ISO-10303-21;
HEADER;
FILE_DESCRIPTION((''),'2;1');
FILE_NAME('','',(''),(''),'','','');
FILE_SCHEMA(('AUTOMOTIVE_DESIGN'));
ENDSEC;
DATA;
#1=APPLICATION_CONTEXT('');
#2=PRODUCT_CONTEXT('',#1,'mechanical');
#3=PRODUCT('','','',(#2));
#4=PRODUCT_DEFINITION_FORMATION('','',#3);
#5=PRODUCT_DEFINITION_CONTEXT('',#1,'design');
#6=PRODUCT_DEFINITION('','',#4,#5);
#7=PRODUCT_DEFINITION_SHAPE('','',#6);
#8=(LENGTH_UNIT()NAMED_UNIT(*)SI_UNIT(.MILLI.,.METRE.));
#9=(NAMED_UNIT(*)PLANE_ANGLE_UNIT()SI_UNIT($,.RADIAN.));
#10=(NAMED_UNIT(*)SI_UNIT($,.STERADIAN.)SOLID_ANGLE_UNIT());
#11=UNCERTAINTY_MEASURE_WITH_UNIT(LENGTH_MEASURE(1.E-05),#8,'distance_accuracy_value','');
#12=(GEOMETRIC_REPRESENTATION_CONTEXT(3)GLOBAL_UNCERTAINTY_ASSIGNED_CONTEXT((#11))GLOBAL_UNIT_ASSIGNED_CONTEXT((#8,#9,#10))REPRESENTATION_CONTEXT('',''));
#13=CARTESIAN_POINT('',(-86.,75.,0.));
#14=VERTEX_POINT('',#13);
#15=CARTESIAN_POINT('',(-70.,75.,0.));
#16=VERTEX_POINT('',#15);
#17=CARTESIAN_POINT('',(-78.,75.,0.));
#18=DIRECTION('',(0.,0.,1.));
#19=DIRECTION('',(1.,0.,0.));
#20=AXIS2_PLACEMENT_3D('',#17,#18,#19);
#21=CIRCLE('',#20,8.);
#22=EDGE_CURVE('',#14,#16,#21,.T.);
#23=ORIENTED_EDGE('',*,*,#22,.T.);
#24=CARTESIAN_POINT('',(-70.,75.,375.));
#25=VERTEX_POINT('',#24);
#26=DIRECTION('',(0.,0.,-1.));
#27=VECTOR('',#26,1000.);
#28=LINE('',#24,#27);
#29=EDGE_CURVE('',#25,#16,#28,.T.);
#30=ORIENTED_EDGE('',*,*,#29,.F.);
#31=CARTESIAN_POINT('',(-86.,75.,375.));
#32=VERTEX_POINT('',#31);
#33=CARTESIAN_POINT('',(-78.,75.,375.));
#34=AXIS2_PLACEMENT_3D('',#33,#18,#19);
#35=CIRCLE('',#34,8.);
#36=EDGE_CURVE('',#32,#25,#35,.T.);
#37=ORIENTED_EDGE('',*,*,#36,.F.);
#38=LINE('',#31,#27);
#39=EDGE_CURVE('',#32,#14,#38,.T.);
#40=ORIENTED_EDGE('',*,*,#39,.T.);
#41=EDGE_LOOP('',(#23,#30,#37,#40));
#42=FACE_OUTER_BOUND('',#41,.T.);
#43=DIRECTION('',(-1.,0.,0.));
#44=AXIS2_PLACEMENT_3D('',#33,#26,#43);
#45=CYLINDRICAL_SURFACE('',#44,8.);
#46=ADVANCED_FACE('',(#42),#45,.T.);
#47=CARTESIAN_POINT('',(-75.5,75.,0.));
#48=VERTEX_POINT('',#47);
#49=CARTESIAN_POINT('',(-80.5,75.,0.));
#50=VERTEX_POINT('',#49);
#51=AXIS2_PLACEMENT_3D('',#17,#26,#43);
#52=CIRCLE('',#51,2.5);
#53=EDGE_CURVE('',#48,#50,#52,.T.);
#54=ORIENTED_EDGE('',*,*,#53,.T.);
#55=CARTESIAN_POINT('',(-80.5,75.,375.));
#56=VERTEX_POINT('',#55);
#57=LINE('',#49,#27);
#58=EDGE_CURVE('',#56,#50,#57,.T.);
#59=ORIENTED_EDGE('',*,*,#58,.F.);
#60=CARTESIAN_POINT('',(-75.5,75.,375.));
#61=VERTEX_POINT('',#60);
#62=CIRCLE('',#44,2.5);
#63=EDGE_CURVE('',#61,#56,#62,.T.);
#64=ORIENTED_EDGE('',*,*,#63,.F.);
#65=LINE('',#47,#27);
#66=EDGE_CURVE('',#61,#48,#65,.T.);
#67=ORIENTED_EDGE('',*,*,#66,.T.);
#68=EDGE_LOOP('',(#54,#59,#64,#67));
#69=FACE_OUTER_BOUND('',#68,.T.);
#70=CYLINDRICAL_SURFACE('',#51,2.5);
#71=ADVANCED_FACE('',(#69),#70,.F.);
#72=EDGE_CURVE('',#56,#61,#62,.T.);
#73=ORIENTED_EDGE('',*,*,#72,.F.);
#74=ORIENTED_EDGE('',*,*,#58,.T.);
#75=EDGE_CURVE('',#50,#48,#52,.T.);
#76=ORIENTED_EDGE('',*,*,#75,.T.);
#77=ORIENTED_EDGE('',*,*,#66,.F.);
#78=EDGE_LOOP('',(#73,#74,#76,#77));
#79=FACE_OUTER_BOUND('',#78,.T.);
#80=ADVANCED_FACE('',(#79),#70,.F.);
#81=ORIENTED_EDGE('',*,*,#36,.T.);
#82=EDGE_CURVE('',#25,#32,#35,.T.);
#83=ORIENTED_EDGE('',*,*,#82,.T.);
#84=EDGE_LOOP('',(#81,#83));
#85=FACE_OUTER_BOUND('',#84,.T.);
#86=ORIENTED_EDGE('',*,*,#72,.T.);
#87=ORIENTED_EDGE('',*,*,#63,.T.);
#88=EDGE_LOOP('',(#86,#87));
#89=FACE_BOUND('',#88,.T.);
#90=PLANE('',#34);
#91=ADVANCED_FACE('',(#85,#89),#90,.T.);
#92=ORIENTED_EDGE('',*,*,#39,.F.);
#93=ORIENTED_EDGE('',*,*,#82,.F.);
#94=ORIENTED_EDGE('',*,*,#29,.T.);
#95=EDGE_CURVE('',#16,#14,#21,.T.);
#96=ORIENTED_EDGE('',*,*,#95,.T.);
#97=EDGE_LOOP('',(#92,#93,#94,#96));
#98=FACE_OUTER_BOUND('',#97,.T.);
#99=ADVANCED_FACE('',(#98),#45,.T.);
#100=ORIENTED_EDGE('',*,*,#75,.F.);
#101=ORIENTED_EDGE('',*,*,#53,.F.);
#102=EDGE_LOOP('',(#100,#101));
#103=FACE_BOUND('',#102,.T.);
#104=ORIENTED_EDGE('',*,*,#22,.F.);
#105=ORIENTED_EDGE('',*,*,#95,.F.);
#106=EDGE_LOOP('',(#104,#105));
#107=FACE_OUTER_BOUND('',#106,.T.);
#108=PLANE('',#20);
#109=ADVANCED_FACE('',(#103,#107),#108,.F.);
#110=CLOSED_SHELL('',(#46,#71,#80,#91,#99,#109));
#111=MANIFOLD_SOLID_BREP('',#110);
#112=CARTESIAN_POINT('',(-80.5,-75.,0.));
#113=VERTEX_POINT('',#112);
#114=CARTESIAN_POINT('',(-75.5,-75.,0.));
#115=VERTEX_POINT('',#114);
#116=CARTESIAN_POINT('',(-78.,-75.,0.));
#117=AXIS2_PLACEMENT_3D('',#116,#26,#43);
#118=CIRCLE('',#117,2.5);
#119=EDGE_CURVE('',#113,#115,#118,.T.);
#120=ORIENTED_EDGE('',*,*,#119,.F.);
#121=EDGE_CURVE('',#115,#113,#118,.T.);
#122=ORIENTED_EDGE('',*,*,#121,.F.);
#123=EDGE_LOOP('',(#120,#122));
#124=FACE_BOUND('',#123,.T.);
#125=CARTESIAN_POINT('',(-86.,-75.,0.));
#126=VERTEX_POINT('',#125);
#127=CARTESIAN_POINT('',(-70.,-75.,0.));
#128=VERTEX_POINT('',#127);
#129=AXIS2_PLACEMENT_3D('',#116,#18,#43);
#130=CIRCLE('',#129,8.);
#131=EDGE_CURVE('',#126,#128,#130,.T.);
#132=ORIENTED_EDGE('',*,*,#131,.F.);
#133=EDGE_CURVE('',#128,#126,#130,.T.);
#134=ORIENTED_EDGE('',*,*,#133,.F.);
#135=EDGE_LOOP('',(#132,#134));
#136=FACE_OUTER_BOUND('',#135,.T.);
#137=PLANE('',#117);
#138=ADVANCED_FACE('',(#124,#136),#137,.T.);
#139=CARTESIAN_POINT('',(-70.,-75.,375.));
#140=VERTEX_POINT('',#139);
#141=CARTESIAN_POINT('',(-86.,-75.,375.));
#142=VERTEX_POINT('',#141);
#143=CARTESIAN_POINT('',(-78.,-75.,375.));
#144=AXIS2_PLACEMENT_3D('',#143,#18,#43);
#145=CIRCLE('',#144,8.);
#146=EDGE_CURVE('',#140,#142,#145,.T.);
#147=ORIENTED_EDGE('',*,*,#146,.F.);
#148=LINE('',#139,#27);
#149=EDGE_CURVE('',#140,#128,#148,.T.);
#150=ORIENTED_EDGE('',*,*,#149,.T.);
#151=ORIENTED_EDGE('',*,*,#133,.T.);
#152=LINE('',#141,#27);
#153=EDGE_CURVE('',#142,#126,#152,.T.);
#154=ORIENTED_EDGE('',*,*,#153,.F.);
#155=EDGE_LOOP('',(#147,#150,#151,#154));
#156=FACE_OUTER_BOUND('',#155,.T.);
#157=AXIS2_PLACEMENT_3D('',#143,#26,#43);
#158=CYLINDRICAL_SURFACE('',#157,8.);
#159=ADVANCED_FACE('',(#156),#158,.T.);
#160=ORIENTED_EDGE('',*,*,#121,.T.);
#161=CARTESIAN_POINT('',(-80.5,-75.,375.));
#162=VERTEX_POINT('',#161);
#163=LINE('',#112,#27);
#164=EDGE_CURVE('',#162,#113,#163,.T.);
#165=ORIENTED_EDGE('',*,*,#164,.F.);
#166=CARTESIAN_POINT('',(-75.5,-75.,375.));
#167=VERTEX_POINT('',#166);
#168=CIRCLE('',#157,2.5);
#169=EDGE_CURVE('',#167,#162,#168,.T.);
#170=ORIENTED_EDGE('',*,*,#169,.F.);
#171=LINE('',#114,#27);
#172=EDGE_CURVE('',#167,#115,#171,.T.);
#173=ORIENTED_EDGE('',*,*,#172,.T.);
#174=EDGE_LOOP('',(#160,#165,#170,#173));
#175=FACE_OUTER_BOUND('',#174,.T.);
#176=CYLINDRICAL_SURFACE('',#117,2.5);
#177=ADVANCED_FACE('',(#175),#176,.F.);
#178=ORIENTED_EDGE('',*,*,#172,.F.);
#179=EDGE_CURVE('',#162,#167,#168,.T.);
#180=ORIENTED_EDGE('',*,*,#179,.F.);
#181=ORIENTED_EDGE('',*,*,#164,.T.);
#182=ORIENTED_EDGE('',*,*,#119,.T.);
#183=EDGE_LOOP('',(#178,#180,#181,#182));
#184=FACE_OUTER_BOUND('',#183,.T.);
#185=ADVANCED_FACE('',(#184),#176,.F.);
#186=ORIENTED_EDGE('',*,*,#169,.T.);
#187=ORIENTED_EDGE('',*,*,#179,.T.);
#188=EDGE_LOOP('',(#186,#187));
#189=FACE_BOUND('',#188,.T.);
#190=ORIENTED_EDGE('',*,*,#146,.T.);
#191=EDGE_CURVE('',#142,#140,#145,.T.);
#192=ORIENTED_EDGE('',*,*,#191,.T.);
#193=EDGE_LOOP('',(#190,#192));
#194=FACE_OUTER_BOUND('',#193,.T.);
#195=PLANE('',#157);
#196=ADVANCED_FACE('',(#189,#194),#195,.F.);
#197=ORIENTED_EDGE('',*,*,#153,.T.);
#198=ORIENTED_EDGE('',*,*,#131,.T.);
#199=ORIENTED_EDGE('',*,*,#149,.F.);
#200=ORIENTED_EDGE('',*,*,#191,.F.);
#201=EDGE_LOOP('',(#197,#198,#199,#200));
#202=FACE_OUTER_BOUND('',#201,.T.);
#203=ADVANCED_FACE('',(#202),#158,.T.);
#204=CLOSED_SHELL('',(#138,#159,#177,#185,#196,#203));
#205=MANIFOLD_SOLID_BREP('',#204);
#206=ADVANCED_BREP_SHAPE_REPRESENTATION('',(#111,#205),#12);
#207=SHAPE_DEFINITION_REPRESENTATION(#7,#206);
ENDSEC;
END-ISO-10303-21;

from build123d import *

# Parameters (mm, degrees)
SKETCH1_R                  = 8
BOSS_EXTRUDE1_DEPTH        = 375
BOSS_EXTRUDE1_2_DEPTH      = 375
SKETCH3_W                  = 2.5
SKETCH3_H                  = 375
M6_TAPPED_HOLE1_AT_2_COUNT = 2
M6_TAPPED_HOLE1_AT_2_PITCH = 150


with BuildPart() as part:
    # Sketch1 → Boss-Extrude1 (new body)
    with BuildSketch(Plane.XY):
        with Locations((-78, 75)):
            Circle(SKETCH1_R)
    extrude(amount=BOSS_EXTRUDE1_DEPTH)

    # Sketch3 → M6 Tapped Hole1 (revolve, cut)
    with BuildSketch(Plane(origin=(-78, 75, 0), x_dir=(0, 1, 0), z_dir=(1, 0, 0))):
        with Locations((1.25, 187.5)):
            Rectangle(SKETCH3_W, SKETCH3_H)
    m6_tapped_hole1 = revolve(axis=Axis((-78, 75, -6.35), (0, 0, 1)), mode=Mode.SUBTRACT)


with BuildPart() as body_2:
    # Sketch1 → Boss-Extrude1 2 (new body)
    with BuildSketch(Plane.XY):
        with Locations(Location((-78, -75, 0), (0, 0, 180))):
            Circle(SKETCH1_R)
    extrude(amount=BOSS_EXTRUDE1_2_DEPTH)

    # M6 Tapped Hole1 at 2: M6 Tapped Hole1 ×2
    with Locations(*[(0, -i * M6_TAPPED_HOLE1_AT_2_PITCH, 0) for i in range(1, M6_TAPPED_HOLE1_AT_2_COUNT)]):
        add(m6_tapped_hole1, mode=Mode.SUBTRACT)


solid = Compound([part.part, body_2.part])
